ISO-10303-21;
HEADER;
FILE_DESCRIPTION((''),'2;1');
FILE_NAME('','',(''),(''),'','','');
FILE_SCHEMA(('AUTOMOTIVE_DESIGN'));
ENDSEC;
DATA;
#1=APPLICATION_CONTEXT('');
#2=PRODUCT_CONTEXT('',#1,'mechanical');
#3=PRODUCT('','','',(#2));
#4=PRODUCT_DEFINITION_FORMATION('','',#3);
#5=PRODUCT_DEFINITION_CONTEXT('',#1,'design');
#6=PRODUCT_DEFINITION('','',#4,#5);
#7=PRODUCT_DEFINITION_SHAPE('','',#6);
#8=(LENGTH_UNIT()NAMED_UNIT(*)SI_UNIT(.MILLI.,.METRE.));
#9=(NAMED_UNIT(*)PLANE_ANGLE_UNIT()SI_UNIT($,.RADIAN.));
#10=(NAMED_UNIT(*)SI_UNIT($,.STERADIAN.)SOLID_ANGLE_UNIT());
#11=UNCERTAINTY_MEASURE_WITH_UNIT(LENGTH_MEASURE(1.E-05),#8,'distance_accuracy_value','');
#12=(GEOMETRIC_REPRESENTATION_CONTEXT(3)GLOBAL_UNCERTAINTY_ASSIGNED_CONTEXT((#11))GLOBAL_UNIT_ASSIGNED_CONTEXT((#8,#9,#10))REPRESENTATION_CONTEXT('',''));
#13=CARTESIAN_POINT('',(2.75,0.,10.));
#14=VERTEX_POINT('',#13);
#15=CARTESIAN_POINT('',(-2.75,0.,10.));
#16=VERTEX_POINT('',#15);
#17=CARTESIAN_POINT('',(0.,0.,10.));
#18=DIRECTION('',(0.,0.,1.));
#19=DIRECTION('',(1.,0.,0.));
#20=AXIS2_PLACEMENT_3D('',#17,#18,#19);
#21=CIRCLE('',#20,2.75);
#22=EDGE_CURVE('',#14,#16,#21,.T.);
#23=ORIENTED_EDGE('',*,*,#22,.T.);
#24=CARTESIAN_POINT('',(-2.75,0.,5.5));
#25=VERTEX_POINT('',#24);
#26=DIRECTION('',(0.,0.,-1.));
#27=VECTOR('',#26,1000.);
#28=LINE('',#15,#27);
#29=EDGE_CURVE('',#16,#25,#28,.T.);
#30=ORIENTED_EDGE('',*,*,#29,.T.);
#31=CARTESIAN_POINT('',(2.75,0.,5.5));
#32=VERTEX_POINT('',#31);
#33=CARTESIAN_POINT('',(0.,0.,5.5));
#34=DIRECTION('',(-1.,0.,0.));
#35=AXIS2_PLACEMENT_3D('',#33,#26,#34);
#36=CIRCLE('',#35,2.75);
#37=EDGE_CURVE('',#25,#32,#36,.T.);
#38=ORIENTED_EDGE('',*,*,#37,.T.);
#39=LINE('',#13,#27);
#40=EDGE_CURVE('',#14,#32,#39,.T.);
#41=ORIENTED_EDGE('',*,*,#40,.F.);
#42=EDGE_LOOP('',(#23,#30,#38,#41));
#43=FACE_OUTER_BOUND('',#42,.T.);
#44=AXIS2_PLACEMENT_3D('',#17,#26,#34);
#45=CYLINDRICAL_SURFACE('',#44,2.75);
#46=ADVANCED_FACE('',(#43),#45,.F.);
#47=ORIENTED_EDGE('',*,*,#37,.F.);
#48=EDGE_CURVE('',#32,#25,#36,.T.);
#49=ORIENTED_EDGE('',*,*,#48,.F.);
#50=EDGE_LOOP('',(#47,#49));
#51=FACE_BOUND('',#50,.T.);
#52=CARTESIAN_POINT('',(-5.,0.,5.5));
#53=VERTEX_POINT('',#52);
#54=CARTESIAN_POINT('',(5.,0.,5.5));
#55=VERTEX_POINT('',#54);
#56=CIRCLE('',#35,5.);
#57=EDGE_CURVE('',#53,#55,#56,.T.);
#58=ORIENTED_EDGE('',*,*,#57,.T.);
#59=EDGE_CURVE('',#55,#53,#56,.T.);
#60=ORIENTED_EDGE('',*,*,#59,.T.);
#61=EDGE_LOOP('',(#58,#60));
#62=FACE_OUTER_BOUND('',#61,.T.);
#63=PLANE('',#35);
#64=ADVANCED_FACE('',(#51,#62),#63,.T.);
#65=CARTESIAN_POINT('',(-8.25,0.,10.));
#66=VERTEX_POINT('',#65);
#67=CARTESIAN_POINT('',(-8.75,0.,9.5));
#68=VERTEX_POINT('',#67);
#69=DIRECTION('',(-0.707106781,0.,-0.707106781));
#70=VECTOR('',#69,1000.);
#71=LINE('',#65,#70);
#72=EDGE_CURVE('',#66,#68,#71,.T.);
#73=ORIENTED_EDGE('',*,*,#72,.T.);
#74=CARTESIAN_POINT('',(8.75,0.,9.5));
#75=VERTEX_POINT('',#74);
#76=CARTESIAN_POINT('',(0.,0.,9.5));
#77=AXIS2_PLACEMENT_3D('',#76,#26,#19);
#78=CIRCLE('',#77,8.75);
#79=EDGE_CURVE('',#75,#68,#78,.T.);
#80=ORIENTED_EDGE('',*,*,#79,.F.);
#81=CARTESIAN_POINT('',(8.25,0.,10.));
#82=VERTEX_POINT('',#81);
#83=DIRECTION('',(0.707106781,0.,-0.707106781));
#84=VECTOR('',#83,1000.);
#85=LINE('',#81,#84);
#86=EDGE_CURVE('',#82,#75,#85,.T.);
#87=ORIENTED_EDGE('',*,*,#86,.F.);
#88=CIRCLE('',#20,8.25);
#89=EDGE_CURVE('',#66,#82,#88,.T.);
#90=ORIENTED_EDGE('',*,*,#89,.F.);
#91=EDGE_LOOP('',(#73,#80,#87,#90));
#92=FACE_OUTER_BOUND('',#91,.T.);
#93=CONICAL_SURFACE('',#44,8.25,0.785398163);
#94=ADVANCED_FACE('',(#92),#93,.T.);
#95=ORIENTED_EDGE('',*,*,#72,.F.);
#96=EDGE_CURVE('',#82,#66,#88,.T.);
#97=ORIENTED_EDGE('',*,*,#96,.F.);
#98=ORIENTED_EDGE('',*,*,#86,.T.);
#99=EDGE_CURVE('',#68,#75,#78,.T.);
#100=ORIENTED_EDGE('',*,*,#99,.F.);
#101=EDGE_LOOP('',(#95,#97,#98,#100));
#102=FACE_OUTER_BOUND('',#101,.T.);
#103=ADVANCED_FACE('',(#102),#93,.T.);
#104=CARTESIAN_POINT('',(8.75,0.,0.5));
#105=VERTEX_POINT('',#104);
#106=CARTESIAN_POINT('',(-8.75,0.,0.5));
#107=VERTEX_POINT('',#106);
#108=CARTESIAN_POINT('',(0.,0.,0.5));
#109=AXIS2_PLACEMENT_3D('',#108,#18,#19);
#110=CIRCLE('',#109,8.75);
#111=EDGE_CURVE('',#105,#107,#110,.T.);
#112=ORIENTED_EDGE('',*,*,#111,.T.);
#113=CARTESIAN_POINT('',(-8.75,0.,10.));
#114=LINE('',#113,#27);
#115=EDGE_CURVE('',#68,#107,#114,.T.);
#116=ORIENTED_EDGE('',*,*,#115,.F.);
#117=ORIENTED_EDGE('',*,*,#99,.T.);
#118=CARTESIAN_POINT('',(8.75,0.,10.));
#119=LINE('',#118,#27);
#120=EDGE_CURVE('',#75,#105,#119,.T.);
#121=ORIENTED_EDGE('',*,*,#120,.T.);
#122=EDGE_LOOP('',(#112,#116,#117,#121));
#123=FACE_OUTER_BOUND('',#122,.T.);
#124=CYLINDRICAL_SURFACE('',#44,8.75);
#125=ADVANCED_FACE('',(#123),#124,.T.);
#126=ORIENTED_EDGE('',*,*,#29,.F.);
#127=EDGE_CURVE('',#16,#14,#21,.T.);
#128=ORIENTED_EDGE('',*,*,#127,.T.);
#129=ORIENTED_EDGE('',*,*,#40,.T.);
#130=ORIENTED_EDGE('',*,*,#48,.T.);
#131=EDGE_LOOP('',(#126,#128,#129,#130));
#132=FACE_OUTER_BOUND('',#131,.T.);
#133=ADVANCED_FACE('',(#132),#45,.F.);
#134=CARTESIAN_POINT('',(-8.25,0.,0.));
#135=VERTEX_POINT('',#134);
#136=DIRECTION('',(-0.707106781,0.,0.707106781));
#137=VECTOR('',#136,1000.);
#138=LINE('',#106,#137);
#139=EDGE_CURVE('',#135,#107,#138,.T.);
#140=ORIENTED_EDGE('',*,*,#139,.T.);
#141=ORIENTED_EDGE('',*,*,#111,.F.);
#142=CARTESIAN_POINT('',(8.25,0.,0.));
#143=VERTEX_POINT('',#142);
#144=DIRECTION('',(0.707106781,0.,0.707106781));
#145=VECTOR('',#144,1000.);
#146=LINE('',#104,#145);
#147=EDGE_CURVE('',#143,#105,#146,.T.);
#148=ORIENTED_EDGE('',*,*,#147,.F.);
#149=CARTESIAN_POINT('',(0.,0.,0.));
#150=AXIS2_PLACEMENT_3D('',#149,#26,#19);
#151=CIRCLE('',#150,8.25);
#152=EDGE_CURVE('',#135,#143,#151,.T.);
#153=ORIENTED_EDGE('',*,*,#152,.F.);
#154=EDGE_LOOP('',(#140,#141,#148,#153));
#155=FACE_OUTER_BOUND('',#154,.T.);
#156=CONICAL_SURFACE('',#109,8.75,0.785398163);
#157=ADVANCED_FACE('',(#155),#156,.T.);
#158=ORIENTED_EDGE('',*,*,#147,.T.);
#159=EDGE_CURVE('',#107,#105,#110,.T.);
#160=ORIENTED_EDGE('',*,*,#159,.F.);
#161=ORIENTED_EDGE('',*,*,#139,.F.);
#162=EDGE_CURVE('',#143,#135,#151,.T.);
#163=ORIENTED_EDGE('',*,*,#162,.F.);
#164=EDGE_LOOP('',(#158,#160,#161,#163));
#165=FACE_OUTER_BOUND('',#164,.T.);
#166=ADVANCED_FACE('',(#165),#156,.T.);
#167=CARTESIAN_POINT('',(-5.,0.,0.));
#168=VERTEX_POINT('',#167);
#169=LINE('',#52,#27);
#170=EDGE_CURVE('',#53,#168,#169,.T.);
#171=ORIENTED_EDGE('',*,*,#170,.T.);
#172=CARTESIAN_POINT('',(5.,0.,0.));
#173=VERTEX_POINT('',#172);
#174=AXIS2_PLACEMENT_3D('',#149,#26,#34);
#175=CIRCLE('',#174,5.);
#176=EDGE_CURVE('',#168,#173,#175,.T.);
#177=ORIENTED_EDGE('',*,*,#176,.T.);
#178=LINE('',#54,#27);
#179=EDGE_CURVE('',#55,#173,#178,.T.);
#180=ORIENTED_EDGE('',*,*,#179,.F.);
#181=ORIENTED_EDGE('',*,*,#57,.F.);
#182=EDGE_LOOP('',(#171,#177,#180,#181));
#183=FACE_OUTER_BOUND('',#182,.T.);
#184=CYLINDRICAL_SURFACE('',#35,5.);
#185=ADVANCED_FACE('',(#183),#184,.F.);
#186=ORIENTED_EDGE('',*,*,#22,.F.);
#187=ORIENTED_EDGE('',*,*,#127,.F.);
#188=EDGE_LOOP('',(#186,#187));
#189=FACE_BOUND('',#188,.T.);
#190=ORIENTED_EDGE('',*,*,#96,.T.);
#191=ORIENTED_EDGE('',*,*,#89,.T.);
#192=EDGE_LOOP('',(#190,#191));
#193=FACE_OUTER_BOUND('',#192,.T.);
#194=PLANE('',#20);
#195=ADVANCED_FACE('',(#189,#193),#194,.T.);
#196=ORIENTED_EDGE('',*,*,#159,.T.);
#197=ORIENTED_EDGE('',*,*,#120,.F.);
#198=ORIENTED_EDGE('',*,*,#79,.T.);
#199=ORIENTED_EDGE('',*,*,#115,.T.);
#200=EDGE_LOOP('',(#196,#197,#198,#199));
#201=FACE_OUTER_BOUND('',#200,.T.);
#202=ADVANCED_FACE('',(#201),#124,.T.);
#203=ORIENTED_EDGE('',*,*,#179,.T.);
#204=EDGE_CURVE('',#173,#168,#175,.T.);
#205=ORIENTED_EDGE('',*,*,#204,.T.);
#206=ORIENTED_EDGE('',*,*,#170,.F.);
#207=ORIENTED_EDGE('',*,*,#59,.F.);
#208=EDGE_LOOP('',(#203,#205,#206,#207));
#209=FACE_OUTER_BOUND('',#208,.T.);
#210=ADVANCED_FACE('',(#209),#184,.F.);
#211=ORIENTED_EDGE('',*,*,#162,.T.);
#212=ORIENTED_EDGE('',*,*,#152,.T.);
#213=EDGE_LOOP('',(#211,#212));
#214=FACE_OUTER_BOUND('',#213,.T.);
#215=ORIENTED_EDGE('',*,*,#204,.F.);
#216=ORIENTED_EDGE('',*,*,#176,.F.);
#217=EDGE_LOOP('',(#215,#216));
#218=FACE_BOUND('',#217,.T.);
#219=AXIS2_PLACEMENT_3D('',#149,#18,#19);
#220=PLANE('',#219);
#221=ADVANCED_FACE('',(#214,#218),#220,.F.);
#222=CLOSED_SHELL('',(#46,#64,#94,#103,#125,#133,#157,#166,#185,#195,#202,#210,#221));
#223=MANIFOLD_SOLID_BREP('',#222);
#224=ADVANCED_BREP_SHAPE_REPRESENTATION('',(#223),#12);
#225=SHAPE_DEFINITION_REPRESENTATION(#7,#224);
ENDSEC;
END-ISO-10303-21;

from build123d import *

# Parameters (mm, degrees)
SKETCH1_R           = 8.75
SKETCH1_R_2         = 2.75
BOSS_EXTRUDE1_DEPTH = 10
SKETCH2_R           = 5
CUT_EXTRUDE1_DEPTH  = 5.5
CHAMFER1_SIZE       = 0.5


with BuildPart() as part:
    # Sketch1 → Boss-Extrude1 (new body)
    with BuildSketch(Plane.XY):
        Circle(SKETCH1_R)
        Circle(SKETCH1_R_2, mode=Mode.SUBTRACT)
    extrude(amount=BOSS_EXTRUDE1_DEPTH)

    # Sketch2 → Cut-Extrude1 (cut)
    with BuildSketch(Plane(origin=(0, 0, 0), x_dir=(-1, 0, 0), z_dir=(0, 0, -1))):
        Circle(SKETCH2_R)
    extrude(amount=-CUT_EXTRUDE1_DEPTH, mode=Mode.SUBTRACT)

    # Chamfer1
    chamfer1_edges = [part.edges().sort_by_distance(p)[0] for p in [
        (-8.75, 0, 0),
        (-8.75, 0, 10),
    ]]
    chamfer(chamfer1_edges, length=CHAMFER1_SIZE)


solid = part.part
